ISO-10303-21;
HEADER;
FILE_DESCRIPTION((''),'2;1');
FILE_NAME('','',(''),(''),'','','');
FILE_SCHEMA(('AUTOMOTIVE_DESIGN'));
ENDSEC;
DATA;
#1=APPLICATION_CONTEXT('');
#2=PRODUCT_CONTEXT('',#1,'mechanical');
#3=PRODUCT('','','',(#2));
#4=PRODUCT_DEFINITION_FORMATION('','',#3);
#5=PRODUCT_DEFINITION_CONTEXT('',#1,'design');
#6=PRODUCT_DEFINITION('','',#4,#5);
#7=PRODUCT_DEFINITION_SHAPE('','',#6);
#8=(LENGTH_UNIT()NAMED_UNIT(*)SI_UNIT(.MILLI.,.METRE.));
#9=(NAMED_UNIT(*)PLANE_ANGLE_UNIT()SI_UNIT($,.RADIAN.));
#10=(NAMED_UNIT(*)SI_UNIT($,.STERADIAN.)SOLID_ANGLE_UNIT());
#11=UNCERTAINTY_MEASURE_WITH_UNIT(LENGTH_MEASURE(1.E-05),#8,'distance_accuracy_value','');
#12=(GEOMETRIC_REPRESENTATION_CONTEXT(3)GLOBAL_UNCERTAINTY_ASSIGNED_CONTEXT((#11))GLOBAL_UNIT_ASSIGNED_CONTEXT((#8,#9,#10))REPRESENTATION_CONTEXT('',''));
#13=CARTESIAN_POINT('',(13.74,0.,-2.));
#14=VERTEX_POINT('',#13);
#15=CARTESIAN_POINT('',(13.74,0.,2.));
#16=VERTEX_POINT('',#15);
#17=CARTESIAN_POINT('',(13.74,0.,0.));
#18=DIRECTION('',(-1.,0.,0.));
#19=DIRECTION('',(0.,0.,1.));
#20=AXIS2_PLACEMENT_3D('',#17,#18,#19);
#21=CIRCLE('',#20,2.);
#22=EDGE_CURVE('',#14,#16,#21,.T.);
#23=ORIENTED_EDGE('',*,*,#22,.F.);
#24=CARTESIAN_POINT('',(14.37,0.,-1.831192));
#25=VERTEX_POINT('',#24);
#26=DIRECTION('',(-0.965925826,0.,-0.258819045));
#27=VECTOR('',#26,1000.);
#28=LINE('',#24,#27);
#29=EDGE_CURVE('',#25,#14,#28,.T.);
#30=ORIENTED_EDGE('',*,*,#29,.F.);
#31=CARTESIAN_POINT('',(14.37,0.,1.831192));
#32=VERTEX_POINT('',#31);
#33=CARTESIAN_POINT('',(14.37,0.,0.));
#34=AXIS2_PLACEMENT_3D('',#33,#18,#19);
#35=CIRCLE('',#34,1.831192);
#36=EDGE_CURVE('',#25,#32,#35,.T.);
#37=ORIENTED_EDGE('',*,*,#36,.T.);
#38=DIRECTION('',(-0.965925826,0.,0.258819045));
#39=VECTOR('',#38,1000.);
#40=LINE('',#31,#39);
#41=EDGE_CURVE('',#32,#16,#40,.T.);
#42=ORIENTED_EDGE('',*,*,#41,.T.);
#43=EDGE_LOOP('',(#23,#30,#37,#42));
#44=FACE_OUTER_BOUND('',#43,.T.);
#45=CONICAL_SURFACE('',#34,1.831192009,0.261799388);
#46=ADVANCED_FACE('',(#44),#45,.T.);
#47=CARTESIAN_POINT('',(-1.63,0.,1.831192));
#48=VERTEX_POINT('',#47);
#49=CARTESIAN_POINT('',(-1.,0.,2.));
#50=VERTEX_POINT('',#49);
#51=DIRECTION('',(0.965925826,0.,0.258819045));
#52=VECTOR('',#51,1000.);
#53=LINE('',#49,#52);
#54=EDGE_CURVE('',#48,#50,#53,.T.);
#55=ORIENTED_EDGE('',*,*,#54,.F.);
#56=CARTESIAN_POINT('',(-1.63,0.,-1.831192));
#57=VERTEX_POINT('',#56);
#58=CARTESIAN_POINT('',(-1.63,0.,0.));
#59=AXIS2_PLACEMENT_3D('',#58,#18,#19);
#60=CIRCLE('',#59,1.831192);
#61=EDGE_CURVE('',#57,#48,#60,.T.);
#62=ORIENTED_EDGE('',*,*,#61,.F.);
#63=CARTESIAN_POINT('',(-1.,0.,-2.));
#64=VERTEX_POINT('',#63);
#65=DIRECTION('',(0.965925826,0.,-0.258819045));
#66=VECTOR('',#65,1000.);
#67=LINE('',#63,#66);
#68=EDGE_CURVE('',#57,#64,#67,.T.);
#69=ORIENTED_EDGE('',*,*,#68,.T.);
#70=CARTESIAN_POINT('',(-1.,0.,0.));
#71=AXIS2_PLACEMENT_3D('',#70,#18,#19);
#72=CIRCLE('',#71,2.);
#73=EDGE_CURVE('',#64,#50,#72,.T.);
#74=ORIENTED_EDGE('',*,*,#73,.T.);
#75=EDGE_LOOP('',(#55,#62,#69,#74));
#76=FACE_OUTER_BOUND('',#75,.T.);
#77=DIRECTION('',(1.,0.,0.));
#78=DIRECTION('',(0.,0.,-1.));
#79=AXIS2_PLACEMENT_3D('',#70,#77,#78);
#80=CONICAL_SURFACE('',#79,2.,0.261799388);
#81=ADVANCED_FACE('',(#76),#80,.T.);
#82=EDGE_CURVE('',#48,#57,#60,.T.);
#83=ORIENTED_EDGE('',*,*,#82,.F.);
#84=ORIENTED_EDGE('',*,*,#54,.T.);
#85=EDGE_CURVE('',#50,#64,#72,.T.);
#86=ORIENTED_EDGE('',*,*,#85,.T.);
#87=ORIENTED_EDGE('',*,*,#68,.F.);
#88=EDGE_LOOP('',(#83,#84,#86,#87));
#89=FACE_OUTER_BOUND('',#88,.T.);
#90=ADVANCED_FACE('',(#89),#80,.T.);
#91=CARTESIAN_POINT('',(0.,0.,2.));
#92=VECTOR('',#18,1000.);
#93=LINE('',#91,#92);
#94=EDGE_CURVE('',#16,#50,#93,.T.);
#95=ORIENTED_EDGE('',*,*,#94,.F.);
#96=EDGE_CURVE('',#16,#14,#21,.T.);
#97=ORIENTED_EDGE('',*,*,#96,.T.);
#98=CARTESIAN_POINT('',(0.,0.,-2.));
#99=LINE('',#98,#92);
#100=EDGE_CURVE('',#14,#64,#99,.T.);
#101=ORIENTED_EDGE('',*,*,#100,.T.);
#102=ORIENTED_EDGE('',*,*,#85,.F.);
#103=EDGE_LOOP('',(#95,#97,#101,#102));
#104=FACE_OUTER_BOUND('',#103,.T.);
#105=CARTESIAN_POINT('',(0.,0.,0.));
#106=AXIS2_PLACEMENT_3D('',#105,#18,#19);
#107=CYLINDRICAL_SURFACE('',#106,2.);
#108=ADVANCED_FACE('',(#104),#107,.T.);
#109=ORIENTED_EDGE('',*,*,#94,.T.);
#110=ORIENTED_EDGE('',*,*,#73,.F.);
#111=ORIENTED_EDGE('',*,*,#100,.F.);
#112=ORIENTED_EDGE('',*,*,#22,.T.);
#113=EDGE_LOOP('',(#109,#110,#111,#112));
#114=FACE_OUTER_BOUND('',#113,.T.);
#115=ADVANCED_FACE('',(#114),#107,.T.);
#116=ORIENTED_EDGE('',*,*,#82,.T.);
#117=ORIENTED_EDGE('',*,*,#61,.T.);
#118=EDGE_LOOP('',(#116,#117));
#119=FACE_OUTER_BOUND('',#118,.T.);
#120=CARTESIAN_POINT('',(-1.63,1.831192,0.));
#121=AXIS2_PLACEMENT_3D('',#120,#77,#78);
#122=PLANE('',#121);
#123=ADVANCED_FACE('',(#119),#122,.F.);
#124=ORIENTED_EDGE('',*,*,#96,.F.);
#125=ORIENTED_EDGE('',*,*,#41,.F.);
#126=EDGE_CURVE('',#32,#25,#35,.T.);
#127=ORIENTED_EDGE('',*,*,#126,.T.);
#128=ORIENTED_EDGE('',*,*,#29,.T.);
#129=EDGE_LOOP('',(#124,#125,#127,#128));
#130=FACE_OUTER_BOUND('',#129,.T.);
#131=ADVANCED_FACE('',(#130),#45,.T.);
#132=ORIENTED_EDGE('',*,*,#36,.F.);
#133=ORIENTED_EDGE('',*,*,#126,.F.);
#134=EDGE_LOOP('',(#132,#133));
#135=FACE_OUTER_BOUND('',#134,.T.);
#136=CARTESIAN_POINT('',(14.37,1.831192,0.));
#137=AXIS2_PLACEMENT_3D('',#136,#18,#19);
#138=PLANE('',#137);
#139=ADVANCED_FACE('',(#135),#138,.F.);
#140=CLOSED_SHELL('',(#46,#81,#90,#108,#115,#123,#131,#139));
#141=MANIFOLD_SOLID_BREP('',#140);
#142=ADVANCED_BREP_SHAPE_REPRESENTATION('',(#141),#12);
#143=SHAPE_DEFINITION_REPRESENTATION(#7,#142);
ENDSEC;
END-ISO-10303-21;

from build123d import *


with BuildPart() as part:
    # Sketch1 → Base-Revolve (revolve)
    with BuildSketch(Plane.XY, mode=Mode.PRIVATE) as base_revolve_sk:
        Polygon((-1.63, 0), (14.37, 0), (14.37, 1.831192009), (13.74, 2), (-1, 2), (-1.63, 1.831192009), align=None)
    revolve(base_revolve_sk.sketch.rotate(Axis((0, 0, 0), (1, 0, 0)), 90), axis=Axis((0, 0, 0), (1, 0, 0)))


solid = part.part
